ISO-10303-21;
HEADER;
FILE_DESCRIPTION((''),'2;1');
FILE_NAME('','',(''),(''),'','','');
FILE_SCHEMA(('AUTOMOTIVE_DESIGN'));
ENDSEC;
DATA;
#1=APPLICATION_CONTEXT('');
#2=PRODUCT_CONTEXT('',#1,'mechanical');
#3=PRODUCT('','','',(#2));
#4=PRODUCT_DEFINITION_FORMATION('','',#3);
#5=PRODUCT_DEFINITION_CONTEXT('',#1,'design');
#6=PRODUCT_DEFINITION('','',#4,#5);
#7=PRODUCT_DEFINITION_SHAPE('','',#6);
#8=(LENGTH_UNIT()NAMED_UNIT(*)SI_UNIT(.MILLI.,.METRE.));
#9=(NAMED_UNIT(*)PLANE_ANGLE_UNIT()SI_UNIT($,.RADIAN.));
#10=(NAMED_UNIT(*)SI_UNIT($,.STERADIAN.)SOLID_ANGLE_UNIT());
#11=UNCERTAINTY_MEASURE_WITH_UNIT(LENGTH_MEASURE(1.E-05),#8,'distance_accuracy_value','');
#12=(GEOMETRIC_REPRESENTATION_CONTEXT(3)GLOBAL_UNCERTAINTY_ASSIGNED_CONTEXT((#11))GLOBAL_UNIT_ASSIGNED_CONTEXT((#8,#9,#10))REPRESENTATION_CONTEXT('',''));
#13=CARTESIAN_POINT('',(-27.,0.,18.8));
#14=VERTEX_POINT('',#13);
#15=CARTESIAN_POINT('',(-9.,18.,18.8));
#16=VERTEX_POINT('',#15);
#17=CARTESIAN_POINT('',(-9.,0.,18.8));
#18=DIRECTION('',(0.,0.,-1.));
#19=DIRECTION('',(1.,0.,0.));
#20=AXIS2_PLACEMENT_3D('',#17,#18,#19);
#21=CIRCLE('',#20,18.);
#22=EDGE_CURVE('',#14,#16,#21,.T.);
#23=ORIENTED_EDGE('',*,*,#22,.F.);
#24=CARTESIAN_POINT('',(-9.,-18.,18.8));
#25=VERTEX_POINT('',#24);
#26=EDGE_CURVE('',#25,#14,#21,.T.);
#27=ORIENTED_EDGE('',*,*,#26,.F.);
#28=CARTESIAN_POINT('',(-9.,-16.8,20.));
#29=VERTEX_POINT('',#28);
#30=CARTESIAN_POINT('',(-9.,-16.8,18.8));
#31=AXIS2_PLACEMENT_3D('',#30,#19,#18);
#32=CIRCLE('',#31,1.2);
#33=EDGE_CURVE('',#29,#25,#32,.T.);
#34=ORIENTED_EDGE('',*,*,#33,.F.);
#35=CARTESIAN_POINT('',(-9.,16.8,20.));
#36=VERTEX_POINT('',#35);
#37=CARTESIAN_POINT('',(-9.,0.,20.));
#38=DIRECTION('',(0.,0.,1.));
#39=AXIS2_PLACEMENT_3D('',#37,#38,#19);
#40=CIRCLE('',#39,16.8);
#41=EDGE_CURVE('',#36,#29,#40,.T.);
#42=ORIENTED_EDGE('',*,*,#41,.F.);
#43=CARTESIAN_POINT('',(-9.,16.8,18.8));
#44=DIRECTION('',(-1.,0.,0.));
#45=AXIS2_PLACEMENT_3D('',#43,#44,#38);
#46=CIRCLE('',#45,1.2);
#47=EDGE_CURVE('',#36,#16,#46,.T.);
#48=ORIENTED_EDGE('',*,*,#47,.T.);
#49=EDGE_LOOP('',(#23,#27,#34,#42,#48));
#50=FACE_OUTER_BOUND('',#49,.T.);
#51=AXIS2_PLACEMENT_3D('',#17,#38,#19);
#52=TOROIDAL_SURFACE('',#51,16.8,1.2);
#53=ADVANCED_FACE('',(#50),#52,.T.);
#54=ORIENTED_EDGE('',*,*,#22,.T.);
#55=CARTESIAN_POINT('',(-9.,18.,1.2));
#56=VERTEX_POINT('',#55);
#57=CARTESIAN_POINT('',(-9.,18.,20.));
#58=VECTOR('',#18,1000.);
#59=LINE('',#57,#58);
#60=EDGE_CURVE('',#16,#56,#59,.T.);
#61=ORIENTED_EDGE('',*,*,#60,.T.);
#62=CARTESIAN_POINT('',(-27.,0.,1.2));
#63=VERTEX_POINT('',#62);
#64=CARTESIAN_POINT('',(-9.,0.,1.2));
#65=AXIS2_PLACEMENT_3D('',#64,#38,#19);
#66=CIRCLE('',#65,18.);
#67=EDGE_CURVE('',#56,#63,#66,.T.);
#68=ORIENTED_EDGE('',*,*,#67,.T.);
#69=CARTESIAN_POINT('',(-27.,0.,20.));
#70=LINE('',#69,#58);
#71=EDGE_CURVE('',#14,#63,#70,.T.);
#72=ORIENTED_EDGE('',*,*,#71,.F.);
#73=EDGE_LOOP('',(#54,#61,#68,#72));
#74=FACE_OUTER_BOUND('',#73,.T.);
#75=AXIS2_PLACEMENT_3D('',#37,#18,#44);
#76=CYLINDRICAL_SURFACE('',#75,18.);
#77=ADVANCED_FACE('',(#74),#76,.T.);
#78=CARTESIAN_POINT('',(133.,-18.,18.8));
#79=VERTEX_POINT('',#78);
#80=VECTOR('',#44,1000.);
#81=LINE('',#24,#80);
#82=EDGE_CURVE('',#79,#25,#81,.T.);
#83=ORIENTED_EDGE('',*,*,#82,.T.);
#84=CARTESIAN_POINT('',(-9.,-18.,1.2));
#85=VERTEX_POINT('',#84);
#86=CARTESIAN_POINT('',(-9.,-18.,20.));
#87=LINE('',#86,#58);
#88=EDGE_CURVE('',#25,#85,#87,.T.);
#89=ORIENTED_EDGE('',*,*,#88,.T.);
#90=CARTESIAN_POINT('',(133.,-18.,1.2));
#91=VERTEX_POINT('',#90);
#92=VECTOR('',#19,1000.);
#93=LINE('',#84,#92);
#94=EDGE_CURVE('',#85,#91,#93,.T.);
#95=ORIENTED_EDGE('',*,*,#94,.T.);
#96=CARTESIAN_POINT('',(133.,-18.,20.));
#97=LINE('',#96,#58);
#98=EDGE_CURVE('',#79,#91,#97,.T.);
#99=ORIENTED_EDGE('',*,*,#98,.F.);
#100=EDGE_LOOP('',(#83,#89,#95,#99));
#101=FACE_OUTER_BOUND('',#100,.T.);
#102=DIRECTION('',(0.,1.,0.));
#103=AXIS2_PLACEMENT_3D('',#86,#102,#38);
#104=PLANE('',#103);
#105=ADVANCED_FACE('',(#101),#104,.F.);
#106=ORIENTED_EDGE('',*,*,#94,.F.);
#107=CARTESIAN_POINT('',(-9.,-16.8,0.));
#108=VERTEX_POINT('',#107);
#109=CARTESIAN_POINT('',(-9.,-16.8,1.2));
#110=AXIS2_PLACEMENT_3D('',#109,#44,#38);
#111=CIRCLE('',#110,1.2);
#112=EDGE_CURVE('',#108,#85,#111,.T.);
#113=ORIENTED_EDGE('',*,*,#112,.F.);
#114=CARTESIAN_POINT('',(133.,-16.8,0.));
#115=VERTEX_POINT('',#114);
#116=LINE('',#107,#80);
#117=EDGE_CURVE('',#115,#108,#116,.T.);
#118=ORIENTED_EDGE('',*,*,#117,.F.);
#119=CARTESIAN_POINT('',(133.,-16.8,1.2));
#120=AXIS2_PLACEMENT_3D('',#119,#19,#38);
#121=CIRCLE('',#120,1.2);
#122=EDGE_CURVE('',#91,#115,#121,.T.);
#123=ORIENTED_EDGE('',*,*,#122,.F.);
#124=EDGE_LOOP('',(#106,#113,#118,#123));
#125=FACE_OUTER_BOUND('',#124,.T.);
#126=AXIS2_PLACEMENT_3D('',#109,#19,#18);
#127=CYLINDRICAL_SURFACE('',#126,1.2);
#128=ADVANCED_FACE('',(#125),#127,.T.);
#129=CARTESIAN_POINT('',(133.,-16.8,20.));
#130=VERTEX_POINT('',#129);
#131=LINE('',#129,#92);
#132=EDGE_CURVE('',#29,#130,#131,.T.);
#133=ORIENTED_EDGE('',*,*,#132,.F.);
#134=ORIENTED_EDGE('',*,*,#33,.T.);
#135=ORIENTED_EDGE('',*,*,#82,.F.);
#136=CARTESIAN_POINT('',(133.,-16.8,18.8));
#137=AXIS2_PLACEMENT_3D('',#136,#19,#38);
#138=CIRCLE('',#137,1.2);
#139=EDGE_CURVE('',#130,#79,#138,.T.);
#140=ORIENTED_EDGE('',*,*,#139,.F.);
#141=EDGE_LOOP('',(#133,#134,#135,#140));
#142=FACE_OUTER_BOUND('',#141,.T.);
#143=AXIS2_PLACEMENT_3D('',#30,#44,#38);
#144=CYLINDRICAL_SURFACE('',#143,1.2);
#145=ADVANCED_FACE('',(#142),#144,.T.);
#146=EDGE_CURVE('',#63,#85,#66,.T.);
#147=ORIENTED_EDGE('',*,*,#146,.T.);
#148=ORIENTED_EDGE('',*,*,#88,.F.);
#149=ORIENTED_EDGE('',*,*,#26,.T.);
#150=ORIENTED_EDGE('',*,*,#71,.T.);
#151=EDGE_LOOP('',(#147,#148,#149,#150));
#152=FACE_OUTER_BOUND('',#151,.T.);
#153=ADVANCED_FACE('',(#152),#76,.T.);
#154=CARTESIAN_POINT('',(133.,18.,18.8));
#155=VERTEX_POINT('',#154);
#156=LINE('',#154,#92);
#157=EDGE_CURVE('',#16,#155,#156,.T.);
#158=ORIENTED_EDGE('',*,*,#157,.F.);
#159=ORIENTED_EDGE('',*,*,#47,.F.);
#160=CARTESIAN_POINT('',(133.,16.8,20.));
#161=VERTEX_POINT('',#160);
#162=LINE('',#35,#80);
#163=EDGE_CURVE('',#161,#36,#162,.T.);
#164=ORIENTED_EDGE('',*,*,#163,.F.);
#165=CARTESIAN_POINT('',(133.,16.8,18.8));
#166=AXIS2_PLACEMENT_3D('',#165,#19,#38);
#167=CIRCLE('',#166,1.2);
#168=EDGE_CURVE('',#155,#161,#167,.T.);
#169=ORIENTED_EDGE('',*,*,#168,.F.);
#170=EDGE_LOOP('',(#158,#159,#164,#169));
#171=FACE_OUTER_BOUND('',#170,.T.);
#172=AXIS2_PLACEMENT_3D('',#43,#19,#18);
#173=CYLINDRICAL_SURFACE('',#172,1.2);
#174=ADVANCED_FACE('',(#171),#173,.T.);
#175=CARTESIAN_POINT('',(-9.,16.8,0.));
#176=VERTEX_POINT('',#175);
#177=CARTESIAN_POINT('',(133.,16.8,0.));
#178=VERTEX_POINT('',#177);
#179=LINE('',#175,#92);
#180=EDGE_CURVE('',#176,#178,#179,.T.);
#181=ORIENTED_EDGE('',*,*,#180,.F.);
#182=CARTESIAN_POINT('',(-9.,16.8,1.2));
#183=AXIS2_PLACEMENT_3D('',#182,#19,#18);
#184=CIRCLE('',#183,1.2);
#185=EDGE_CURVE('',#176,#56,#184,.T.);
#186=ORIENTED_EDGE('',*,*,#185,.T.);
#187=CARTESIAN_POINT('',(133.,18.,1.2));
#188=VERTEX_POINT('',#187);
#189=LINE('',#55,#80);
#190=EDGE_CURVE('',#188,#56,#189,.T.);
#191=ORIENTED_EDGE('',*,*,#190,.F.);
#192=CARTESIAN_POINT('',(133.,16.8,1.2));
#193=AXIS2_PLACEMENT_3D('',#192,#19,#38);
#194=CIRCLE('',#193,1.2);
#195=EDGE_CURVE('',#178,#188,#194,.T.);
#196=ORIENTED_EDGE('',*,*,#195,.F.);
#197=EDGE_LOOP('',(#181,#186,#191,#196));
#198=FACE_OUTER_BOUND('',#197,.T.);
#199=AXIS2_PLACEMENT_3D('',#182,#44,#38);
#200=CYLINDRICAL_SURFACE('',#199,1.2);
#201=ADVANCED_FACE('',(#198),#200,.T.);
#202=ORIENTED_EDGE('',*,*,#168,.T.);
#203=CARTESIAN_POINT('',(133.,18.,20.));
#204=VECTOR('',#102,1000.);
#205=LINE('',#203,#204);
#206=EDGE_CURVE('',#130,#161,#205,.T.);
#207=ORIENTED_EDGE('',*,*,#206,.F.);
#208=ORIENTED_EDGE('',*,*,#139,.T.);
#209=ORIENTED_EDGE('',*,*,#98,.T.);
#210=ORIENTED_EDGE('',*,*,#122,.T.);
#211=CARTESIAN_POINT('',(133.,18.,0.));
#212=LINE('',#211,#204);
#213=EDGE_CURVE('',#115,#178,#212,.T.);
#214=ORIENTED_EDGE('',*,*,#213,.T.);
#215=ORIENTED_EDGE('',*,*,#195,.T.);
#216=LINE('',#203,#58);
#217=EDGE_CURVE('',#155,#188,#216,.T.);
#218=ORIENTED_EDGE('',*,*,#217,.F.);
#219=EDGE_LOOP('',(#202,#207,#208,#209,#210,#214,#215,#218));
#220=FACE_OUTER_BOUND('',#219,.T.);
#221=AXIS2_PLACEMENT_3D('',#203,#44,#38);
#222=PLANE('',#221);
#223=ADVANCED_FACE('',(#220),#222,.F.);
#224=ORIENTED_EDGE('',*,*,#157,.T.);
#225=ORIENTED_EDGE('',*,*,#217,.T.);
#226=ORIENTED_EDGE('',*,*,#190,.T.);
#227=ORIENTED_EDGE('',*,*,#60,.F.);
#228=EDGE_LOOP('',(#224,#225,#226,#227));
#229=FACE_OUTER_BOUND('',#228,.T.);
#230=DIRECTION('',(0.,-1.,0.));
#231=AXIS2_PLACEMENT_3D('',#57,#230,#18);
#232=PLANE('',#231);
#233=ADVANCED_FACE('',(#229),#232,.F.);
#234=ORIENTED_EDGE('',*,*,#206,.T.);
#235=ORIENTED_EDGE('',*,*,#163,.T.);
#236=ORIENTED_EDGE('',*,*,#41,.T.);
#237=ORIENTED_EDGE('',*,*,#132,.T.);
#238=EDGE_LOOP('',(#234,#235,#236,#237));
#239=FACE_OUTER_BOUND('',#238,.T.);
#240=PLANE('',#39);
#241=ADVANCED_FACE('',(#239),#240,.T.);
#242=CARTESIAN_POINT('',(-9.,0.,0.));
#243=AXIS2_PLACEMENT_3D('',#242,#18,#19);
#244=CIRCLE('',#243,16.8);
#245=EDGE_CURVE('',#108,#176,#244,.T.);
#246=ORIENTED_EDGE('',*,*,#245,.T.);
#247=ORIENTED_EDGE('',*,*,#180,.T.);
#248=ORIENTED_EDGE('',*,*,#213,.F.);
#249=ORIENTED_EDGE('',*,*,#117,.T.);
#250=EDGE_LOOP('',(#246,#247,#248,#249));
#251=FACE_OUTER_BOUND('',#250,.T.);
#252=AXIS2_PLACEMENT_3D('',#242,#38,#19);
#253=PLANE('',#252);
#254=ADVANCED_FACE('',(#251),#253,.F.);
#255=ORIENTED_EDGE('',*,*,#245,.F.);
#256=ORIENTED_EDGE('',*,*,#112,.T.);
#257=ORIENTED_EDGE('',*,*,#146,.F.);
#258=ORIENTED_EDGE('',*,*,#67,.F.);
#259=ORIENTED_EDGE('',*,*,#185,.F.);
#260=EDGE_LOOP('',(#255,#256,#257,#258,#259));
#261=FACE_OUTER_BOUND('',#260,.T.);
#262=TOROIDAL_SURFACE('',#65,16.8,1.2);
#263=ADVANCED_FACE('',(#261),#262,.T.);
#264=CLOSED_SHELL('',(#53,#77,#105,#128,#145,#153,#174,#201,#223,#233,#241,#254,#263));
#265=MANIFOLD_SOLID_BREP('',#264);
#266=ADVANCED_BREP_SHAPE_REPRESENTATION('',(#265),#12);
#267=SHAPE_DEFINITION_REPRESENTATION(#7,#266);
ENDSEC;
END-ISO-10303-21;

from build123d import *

# Parameters (mm, degrees)
BASE_EXTRUDE_DEPTH = 20
FILLET1_R          = 1.2


with BuildPart() as part:
    # Sketch1 → Base-Extrude (new body)
    with BuildSketch(Plane.XY):
        with BuildLine():
            Line((-9, 18), (133, 18))
            Line((133, 18), (133, -18))
            Line((133, -18), (-9, -18))
            ThreePointArc((-9, -18), (-27, 0), (-9, 18))
        make_face()
    extrude(amount=BASE_EXTRUDE_DEPTH)

    # Fillet1
    fillet1_edges = [part.edges().sort_by_distance(p)[0] for p in [
        (-27, 0, 20),
        (62, -18, 20),
        (62, -18, 0),
        (-27, 0, 0),
        (62, 18, 0),
        (62, 18, 20),
    ]]
    fillet(fillet1_edges, radius=FILLET1_R)


solid = part.part
